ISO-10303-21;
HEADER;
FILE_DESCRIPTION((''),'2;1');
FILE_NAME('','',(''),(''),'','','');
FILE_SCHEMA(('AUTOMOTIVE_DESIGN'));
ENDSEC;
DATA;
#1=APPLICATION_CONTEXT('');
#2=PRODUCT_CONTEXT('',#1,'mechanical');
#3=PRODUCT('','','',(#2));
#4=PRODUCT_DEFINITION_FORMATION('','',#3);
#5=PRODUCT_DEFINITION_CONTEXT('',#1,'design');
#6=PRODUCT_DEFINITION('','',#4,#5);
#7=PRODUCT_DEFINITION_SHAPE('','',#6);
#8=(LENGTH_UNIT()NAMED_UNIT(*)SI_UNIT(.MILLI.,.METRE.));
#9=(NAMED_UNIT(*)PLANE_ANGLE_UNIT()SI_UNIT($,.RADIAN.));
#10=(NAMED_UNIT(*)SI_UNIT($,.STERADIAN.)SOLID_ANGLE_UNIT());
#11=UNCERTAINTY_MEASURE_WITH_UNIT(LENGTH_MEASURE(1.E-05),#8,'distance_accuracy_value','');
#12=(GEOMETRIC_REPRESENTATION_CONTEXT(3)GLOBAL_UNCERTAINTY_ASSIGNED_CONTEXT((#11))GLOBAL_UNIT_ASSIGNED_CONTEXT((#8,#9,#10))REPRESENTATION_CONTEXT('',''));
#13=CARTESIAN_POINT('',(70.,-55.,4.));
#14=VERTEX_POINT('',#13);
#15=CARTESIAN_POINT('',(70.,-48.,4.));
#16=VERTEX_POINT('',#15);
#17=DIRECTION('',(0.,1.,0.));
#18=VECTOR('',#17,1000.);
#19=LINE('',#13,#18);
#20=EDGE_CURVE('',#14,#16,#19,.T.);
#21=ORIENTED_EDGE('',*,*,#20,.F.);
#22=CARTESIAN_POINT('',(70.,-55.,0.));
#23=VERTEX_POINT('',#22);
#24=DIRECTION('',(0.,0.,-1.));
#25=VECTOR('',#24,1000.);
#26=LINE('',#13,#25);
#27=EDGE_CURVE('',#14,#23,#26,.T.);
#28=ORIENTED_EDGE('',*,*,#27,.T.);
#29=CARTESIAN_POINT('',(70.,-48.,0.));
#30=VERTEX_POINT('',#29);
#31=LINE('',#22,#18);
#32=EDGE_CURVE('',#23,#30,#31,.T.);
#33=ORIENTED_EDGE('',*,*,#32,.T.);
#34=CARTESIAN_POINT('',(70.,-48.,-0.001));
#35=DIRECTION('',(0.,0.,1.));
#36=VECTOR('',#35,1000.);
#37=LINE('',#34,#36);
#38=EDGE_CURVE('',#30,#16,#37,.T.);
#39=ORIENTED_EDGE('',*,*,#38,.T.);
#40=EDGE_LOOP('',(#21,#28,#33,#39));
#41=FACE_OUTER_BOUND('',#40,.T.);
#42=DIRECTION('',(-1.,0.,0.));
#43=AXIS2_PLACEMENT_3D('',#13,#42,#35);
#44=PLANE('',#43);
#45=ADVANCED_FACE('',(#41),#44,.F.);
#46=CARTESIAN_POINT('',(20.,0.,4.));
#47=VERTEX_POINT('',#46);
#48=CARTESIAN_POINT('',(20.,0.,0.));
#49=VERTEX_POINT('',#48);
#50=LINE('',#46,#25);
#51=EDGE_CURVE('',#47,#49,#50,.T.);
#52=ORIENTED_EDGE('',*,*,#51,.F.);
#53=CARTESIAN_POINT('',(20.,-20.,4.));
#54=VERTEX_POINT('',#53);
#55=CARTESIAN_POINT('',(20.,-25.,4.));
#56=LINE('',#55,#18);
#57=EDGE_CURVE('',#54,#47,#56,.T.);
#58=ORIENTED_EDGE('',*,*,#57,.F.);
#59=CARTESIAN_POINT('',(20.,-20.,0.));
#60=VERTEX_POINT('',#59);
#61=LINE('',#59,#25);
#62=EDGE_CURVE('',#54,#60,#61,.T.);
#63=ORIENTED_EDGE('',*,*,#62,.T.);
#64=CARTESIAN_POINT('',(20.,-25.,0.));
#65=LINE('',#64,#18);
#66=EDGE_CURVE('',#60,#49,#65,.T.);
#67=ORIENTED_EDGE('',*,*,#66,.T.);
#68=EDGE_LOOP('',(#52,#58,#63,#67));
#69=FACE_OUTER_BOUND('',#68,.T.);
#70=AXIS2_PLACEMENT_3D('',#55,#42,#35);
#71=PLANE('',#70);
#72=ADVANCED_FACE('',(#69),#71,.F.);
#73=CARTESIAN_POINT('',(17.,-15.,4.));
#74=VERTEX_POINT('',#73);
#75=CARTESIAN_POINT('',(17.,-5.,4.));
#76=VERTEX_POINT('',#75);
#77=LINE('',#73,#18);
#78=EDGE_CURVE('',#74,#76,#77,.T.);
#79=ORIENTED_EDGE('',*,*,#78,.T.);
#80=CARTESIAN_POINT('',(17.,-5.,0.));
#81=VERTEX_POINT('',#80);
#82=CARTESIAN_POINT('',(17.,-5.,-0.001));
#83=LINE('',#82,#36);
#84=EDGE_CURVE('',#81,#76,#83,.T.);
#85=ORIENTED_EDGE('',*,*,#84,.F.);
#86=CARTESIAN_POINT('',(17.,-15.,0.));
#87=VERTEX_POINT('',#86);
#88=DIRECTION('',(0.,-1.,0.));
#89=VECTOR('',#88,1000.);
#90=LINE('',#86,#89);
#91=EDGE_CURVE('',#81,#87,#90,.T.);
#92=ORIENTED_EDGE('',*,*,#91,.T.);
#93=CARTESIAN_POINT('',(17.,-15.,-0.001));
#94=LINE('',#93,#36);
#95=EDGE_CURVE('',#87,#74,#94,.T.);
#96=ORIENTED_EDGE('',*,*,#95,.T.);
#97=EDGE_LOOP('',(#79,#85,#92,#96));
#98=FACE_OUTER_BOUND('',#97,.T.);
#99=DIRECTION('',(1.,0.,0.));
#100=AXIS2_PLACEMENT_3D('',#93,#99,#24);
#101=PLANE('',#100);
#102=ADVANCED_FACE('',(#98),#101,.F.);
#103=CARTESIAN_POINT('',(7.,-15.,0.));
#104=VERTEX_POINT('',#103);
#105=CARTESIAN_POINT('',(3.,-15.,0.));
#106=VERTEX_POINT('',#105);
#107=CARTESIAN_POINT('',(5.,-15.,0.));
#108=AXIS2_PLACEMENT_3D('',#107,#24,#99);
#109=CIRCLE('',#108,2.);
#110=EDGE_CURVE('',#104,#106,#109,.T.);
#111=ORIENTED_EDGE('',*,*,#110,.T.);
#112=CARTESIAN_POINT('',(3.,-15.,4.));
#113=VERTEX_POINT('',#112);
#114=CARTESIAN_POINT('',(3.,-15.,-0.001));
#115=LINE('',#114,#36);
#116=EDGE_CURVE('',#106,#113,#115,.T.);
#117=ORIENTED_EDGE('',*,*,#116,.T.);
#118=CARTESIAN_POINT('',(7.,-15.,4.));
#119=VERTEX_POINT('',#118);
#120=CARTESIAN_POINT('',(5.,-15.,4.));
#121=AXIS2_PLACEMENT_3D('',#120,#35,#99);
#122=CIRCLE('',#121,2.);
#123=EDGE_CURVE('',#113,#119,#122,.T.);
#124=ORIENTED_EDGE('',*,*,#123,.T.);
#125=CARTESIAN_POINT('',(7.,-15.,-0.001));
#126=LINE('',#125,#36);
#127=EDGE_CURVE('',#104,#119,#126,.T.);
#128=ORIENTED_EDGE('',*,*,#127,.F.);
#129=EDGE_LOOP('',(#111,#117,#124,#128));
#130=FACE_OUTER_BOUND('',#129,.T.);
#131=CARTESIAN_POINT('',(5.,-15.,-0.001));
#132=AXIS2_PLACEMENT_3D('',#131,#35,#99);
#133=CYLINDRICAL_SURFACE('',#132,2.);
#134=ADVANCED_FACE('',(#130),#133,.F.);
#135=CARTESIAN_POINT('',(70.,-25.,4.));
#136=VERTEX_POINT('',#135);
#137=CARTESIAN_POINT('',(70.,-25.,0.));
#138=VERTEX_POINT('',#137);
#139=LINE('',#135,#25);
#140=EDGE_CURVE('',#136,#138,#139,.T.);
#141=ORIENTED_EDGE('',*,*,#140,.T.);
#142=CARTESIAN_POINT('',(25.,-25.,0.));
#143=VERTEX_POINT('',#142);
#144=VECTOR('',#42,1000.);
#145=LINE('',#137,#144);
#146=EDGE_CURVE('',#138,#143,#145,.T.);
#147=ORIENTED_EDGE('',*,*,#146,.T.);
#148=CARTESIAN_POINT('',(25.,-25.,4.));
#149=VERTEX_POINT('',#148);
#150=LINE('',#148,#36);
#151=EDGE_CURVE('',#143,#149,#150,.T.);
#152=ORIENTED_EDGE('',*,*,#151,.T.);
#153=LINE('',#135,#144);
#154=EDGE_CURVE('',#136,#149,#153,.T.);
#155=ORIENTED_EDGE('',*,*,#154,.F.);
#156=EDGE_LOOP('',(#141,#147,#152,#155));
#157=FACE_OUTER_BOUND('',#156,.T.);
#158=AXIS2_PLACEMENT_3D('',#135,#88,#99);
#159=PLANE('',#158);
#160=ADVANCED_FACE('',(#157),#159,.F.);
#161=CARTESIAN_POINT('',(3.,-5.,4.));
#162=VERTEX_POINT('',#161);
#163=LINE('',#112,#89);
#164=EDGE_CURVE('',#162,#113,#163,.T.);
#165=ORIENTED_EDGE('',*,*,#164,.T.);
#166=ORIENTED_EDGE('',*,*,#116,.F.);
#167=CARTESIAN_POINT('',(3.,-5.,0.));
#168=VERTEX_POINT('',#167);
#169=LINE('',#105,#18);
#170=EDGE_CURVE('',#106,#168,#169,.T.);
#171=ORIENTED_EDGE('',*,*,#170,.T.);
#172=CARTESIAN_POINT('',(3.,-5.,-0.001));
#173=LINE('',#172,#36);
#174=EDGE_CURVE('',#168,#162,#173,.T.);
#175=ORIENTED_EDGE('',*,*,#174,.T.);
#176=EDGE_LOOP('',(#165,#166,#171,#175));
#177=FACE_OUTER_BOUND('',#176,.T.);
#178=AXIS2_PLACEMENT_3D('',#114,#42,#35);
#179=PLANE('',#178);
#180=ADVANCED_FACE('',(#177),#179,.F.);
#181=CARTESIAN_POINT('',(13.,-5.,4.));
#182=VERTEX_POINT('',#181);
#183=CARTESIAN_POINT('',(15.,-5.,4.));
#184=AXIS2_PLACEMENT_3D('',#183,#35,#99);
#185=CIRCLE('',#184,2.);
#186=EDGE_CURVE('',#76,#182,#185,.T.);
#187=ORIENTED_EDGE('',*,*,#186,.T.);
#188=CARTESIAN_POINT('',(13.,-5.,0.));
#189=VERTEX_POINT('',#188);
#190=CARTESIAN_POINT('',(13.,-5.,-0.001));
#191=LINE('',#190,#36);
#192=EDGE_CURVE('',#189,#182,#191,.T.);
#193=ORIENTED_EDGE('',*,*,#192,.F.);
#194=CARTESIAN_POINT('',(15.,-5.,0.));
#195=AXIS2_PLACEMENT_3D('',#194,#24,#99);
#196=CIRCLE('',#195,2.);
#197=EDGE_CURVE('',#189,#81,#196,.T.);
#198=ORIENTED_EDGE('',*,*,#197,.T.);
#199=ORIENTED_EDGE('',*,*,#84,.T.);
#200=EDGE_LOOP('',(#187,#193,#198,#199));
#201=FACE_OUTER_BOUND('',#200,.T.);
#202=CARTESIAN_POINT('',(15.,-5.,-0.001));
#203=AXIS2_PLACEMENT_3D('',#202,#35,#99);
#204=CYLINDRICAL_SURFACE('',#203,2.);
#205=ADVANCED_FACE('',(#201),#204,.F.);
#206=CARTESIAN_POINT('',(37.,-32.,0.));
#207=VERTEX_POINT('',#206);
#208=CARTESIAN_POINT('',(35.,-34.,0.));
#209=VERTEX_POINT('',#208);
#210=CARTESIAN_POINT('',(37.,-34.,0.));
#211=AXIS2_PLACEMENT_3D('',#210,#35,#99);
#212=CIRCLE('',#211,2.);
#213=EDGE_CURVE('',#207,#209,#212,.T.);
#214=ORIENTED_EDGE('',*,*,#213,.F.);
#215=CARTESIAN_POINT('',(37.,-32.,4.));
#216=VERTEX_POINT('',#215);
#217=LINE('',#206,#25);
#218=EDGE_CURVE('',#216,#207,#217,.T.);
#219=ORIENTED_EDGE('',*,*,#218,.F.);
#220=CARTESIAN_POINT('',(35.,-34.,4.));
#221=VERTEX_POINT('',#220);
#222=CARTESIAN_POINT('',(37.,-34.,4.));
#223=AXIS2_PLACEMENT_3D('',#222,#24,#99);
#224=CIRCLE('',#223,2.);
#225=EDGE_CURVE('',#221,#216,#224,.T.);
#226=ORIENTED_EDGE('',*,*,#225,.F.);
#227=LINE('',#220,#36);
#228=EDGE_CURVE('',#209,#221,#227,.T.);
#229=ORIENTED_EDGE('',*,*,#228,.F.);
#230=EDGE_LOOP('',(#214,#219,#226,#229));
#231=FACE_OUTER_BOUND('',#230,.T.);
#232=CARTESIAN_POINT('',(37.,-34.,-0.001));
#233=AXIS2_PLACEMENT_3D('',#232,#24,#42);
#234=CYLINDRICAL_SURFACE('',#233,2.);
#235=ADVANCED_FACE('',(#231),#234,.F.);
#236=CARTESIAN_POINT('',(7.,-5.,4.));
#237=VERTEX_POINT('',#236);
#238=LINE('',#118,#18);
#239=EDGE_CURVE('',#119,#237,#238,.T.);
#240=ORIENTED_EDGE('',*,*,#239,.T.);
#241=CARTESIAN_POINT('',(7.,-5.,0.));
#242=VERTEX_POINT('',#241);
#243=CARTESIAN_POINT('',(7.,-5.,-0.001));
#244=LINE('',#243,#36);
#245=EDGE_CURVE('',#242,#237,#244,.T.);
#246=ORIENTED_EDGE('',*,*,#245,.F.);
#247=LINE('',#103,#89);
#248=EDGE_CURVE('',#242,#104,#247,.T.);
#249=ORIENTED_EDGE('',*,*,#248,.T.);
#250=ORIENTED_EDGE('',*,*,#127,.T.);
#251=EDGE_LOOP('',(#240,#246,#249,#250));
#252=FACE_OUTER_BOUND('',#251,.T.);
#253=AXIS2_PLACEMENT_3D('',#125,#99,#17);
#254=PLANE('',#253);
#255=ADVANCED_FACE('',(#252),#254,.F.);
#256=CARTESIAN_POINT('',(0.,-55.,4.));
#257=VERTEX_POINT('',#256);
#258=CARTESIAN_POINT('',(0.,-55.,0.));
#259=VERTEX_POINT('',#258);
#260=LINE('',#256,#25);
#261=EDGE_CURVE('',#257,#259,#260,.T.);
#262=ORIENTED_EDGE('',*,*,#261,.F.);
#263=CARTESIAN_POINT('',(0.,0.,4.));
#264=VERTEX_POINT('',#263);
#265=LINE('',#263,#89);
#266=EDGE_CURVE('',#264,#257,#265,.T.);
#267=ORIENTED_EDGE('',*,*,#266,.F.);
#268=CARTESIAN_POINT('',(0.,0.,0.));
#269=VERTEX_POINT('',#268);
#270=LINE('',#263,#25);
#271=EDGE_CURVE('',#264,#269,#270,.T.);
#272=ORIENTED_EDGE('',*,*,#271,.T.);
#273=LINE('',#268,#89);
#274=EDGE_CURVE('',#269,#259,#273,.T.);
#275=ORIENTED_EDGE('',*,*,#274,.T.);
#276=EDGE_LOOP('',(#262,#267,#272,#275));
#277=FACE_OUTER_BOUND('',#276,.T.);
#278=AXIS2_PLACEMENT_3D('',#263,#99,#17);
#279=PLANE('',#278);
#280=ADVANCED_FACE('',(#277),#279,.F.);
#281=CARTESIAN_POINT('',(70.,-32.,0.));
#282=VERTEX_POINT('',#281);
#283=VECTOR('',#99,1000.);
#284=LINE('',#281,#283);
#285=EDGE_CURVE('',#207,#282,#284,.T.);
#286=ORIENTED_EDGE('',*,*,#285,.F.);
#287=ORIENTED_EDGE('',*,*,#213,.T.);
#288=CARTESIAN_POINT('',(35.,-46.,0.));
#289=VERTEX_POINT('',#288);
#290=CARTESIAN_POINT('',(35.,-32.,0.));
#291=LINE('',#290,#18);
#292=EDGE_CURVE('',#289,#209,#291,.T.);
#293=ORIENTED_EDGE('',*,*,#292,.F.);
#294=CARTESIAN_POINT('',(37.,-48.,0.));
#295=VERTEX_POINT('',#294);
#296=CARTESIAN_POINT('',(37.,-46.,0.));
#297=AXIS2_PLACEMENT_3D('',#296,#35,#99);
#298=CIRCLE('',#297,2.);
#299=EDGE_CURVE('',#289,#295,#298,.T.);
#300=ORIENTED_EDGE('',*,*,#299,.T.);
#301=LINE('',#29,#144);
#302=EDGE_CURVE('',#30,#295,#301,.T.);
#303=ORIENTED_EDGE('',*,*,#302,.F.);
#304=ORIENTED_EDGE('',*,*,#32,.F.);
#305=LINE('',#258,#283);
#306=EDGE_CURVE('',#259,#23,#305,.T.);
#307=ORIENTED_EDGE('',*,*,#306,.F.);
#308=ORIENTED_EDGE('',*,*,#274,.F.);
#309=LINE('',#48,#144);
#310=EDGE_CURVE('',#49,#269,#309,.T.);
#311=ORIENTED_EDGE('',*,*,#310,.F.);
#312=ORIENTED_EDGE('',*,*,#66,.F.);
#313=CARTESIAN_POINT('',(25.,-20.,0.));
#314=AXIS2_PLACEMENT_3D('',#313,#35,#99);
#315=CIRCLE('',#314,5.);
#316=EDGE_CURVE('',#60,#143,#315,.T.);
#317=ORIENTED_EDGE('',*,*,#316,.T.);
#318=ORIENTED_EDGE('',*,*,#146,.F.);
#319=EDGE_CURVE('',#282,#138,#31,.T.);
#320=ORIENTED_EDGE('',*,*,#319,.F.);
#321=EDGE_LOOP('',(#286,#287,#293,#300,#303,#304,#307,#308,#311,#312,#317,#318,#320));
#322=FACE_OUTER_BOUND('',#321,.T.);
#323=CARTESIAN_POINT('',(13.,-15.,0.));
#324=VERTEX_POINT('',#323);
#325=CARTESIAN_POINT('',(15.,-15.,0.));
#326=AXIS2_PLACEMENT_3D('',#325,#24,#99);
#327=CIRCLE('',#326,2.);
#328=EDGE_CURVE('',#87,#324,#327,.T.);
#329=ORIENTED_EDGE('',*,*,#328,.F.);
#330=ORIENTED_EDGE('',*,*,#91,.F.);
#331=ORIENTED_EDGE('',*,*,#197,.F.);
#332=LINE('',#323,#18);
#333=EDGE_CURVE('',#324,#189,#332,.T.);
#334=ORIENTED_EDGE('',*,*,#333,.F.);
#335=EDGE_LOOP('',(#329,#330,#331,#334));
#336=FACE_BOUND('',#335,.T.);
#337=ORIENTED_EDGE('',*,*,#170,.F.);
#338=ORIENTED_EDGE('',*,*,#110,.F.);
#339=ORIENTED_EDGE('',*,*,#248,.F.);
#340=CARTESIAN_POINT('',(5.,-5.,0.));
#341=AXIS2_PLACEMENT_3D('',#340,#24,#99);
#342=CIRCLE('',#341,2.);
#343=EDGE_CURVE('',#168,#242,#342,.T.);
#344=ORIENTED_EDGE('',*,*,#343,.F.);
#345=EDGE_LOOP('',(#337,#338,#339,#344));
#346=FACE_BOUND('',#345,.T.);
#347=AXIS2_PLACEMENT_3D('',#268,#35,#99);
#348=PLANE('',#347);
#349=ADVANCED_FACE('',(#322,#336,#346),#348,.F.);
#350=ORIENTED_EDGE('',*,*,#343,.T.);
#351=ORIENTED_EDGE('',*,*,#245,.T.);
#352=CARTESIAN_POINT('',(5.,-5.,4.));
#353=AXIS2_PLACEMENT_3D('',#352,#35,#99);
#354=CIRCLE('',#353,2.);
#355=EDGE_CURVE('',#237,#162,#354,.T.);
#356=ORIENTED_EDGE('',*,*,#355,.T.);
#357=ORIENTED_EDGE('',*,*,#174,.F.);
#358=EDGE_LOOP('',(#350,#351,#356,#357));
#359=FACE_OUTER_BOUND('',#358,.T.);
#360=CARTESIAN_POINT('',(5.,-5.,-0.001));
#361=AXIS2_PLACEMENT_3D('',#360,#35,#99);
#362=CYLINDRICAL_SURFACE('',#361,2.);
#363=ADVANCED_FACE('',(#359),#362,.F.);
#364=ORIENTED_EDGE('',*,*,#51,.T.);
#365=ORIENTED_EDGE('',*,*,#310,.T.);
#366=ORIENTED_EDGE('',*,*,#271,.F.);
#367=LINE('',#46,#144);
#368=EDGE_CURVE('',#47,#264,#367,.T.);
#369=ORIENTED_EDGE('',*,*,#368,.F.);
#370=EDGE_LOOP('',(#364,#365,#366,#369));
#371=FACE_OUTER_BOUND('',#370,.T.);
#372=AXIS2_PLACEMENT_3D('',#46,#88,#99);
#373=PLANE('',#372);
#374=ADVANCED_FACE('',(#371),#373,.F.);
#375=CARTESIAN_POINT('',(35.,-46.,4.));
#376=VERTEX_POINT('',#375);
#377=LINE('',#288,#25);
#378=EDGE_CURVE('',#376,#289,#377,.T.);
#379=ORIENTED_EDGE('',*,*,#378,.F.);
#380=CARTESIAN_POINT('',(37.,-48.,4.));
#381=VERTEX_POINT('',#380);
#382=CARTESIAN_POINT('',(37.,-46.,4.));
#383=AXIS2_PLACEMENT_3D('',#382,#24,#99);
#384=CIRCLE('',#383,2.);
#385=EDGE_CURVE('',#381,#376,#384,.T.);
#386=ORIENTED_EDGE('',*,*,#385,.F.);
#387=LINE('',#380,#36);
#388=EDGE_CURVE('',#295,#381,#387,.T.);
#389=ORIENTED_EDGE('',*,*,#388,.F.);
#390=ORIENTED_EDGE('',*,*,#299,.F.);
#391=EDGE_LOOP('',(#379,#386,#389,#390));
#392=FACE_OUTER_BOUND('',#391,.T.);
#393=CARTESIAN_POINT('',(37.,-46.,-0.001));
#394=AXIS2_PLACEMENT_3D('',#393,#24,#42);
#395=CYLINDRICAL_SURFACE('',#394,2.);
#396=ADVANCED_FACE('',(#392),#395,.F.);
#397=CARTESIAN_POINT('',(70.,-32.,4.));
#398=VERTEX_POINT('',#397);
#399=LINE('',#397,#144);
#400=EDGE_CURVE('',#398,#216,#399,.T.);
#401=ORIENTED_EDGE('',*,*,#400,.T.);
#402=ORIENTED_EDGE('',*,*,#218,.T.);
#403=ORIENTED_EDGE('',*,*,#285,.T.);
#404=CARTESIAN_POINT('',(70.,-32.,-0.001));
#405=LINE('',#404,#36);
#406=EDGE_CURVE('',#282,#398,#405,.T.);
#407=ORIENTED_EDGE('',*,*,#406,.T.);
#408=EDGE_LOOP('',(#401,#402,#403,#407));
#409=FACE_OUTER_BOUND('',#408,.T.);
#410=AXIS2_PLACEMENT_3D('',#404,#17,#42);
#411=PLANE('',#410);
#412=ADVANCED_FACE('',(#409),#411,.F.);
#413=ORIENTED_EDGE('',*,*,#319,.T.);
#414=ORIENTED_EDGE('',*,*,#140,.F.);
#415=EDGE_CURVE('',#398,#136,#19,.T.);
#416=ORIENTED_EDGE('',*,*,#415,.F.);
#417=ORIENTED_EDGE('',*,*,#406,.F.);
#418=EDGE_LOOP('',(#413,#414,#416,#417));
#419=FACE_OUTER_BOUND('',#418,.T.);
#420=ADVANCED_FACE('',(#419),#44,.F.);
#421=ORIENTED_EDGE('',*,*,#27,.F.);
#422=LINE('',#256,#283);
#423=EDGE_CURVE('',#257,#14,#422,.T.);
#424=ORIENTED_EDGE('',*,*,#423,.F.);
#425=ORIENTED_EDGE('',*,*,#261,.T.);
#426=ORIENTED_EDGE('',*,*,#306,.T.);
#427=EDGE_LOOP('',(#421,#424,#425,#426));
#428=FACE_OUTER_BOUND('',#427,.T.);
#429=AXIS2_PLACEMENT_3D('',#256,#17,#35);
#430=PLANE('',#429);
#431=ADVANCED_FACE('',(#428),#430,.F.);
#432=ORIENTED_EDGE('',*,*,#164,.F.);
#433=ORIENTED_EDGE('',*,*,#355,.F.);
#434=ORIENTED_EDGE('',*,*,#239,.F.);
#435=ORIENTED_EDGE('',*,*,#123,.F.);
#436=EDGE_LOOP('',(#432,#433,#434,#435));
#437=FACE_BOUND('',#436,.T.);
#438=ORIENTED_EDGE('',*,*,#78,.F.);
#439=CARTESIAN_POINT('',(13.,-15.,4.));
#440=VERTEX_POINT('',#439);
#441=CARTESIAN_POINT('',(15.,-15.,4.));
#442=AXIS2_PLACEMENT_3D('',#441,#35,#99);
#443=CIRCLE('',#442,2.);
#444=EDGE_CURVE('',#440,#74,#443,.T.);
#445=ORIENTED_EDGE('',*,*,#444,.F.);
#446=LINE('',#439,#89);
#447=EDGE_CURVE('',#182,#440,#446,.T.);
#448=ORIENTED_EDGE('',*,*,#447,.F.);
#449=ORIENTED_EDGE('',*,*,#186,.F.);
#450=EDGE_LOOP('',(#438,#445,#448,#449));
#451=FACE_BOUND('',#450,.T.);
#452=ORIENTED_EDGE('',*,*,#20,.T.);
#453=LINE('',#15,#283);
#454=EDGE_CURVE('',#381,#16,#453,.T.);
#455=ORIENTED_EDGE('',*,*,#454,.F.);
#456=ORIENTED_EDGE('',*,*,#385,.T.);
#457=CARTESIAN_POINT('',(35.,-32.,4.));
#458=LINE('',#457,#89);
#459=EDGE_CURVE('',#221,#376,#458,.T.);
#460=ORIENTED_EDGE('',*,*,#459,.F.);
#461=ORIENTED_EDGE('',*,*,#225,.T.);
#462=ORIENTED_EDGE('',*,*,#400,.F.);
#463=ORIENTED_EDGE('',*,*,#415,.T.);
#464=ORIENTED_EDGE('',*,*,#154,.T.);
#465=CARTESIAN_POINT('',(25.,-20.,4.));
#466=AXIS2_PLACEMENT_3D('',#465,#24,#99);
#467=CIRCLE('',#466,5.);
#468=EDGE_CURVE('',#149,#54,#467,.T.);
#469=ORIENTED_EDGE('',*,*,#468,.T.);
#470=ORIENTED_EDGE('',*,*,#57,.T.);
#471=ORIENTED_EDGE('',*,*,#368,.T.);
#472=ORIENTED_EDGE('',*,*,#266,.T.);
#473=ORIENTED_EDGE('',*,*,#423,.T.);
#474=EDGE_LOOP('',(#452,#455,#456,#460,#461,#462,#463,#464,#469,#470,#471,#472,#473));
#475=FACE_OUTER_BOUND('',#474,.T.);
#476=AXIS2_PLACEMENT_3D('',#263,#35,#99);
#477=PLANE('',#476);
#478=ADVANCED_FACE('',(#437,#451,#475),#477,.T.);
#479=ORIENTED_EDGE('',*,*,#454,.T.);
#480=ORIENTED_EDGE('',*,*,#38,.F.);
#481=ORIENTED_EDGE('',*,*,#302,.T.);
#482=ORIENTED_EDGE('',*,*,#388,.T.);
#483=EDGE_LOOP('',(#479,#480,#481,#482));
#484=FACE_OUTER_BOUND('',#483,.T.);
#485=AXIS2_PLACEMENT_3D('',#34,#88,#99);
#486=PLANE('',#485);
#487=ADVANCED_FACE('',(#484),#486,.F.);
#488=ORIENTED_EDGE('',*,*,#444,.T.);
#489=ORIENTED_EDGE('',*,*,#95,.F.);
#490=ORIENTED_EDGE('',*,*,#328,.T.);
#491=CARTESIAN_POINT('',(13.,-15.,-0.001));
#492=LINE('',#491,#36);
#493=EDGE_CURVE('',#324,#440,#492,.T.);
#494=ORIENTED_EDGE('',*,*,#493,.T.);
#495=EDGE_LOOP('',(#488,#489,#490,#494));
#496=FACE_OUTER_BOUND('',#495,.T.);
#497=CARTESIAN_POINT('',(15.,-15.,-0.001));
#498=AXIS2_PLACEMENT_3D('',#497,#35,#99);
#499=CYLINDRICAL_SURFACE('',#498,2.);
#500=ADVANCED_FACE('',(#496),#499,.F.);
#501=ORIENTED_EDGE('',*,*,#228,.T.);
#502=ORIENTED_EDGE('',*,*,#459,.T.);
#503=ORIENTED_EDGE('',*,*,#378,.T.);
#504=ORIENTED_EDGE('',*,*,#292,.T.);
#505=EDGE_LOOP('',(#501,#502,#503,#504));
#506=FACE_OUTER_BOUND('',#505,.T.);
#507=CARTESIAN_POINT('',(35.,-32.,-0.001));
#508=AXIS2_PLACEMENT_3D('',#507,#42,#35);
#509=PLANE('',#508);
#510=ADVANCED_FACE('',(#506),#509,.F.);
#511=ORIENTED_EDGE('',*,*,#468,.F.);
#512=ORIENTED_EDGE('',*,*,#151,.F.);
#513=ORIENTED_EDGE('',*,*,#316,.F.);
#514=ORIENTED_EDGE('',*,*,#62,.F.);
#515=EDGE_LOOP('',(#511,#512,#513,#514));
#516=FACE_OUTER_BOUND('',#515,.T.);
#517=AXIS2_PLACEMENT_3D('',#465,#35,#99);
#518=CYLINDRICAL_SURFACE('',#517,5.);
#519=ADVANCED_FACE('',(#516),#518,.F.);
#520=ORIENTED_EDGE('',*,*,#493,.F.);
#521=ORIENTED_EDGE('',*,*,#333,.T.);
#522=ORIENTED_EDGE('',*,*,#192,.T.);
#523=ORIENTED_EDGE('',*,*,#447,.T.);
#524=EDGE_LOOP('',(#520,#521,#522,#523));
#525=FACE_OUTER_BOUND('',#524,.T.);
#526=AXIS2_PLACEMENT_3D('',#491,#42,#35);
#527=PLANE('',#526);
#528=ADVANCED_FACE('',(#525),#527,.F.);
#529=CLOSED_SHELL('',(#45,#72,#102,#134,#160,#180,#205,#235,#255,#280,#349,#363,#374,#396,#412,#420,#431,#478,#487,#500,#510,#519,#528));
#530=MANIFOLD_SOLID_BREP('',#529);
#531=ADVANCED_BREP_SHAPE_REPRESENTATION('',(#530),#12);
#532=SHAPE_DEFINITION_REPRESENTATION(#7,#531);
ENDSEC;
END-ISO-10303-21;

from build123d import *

# Parameters (mm, degrees)
EXTRUDE_1_DEPTH     = 4
CUT_EXTRUDE_1_REACH = 91.112
FILLET_1_R          = 5
CUT_EXTRUDE_2_REACH = 91.112
SKETCH_3_W          = 35
SKETCH_3_H          = 16
FILLET_2_R          = 2


with BuildPart() as part:
    # 草图1 → 凸台-拉伸1 (new body)
    with BuildSketch(Plane.XY):
        Polygon((0, 0), (0, -55), (70, -55), (70, -25), (20, -25), (20, 0), align=None)
    extrude(amount=EXTRUDE_1_DEPTH)

    # 草图2 → 切除-拉伸1 (cut, up to next)
    with BuildSketch(Plane.XY.offset(4), mode=Mode.PRIVATE) as cut_extrude_1_sk1:
        with BuildLine():
            Line((3, -15), (3, -5))
            ThreePointArc((3, -5), (5, -3), (7, -5))
            Line((7, -5), (7, -15))
            ThreePointArc((7, -15), (5, -17), (3, -15))
        make_face()
    cut_extrude_1_tool1 = extrude(cut_extrude_1_sk1.sketch, amount=-CUT_EXTRUDE_1_REACH, mode=Mode.PRIVATE) & part.part
    # 草图2 → 切除-拉伸1 (cut, up to next)
    with BuildSketch(Plane.XY.offset(4), mode=Mode.PRIVATE) as cut_extrude_1_sk2:
        with BuildLine():
            Line((13, -15), (13, -5))
            ThreePointArc((13, -5), (15, -3), (17, -5))
            Line((17, -5), (17, -15))
            ThreePointArc((17, -15), (15, -17), (13, -15))
        make_face()
    cut_extrude_1_tool2 = extrude(cut_extrude_1_sk2.sketch, amount=-CUT_EXTRUDE_1_REACH, mode=Mode.PRIVATE) & part.part
    add(cut_extrude_1_tool1.solids().sort_by_distance((5, -10, 4))[0], mode=Mode.SUBTRACT)
    add(cut_extrude_1_tool2.solids().sort_by_distance((15, -10, 4))[0], mode=Mode.SUBTRACT)

    # 圆角1
    fillet_1_edges = [part.edges().sort_by_distance(p)[0] for p in [
        (20, -25, 2),
    ]]
    fillet(fillet_1_edges, radius=FILLET_1_R)

    # 草图3 → 切除-拉伸2 (cut, up to next)
    with BuildSketch(Plane.XY.offset(4), mode=Mode.PRIVATE) as cut_extrude_2_sk1:
        with Locations((52.5, -40)):
            Rectangle(SKETCH_3_W, SKETCH_3_H)
    cut_extrude_2_tool1 = extrude(cut_extrude_2_sk1.sketch, amount=-CUT_EXTRUDE_2_REACH, mode=Mode.PRIVATE) & part.part
    add(cut_extrude_2_tool1.solids().sort_by_distance((52.5, -40, 4))[0], mode=Mode.SUBTRACT)

    # 圆角2
    fillet_2_edges = [part.edges().sort_by_distance(p)[0] for p in [
        (35, -48, 2),
        (35, -32, 2),
    ]]
    fillet(fillet_2_edges, radius=FILLET_2_R)


solid = part.part
